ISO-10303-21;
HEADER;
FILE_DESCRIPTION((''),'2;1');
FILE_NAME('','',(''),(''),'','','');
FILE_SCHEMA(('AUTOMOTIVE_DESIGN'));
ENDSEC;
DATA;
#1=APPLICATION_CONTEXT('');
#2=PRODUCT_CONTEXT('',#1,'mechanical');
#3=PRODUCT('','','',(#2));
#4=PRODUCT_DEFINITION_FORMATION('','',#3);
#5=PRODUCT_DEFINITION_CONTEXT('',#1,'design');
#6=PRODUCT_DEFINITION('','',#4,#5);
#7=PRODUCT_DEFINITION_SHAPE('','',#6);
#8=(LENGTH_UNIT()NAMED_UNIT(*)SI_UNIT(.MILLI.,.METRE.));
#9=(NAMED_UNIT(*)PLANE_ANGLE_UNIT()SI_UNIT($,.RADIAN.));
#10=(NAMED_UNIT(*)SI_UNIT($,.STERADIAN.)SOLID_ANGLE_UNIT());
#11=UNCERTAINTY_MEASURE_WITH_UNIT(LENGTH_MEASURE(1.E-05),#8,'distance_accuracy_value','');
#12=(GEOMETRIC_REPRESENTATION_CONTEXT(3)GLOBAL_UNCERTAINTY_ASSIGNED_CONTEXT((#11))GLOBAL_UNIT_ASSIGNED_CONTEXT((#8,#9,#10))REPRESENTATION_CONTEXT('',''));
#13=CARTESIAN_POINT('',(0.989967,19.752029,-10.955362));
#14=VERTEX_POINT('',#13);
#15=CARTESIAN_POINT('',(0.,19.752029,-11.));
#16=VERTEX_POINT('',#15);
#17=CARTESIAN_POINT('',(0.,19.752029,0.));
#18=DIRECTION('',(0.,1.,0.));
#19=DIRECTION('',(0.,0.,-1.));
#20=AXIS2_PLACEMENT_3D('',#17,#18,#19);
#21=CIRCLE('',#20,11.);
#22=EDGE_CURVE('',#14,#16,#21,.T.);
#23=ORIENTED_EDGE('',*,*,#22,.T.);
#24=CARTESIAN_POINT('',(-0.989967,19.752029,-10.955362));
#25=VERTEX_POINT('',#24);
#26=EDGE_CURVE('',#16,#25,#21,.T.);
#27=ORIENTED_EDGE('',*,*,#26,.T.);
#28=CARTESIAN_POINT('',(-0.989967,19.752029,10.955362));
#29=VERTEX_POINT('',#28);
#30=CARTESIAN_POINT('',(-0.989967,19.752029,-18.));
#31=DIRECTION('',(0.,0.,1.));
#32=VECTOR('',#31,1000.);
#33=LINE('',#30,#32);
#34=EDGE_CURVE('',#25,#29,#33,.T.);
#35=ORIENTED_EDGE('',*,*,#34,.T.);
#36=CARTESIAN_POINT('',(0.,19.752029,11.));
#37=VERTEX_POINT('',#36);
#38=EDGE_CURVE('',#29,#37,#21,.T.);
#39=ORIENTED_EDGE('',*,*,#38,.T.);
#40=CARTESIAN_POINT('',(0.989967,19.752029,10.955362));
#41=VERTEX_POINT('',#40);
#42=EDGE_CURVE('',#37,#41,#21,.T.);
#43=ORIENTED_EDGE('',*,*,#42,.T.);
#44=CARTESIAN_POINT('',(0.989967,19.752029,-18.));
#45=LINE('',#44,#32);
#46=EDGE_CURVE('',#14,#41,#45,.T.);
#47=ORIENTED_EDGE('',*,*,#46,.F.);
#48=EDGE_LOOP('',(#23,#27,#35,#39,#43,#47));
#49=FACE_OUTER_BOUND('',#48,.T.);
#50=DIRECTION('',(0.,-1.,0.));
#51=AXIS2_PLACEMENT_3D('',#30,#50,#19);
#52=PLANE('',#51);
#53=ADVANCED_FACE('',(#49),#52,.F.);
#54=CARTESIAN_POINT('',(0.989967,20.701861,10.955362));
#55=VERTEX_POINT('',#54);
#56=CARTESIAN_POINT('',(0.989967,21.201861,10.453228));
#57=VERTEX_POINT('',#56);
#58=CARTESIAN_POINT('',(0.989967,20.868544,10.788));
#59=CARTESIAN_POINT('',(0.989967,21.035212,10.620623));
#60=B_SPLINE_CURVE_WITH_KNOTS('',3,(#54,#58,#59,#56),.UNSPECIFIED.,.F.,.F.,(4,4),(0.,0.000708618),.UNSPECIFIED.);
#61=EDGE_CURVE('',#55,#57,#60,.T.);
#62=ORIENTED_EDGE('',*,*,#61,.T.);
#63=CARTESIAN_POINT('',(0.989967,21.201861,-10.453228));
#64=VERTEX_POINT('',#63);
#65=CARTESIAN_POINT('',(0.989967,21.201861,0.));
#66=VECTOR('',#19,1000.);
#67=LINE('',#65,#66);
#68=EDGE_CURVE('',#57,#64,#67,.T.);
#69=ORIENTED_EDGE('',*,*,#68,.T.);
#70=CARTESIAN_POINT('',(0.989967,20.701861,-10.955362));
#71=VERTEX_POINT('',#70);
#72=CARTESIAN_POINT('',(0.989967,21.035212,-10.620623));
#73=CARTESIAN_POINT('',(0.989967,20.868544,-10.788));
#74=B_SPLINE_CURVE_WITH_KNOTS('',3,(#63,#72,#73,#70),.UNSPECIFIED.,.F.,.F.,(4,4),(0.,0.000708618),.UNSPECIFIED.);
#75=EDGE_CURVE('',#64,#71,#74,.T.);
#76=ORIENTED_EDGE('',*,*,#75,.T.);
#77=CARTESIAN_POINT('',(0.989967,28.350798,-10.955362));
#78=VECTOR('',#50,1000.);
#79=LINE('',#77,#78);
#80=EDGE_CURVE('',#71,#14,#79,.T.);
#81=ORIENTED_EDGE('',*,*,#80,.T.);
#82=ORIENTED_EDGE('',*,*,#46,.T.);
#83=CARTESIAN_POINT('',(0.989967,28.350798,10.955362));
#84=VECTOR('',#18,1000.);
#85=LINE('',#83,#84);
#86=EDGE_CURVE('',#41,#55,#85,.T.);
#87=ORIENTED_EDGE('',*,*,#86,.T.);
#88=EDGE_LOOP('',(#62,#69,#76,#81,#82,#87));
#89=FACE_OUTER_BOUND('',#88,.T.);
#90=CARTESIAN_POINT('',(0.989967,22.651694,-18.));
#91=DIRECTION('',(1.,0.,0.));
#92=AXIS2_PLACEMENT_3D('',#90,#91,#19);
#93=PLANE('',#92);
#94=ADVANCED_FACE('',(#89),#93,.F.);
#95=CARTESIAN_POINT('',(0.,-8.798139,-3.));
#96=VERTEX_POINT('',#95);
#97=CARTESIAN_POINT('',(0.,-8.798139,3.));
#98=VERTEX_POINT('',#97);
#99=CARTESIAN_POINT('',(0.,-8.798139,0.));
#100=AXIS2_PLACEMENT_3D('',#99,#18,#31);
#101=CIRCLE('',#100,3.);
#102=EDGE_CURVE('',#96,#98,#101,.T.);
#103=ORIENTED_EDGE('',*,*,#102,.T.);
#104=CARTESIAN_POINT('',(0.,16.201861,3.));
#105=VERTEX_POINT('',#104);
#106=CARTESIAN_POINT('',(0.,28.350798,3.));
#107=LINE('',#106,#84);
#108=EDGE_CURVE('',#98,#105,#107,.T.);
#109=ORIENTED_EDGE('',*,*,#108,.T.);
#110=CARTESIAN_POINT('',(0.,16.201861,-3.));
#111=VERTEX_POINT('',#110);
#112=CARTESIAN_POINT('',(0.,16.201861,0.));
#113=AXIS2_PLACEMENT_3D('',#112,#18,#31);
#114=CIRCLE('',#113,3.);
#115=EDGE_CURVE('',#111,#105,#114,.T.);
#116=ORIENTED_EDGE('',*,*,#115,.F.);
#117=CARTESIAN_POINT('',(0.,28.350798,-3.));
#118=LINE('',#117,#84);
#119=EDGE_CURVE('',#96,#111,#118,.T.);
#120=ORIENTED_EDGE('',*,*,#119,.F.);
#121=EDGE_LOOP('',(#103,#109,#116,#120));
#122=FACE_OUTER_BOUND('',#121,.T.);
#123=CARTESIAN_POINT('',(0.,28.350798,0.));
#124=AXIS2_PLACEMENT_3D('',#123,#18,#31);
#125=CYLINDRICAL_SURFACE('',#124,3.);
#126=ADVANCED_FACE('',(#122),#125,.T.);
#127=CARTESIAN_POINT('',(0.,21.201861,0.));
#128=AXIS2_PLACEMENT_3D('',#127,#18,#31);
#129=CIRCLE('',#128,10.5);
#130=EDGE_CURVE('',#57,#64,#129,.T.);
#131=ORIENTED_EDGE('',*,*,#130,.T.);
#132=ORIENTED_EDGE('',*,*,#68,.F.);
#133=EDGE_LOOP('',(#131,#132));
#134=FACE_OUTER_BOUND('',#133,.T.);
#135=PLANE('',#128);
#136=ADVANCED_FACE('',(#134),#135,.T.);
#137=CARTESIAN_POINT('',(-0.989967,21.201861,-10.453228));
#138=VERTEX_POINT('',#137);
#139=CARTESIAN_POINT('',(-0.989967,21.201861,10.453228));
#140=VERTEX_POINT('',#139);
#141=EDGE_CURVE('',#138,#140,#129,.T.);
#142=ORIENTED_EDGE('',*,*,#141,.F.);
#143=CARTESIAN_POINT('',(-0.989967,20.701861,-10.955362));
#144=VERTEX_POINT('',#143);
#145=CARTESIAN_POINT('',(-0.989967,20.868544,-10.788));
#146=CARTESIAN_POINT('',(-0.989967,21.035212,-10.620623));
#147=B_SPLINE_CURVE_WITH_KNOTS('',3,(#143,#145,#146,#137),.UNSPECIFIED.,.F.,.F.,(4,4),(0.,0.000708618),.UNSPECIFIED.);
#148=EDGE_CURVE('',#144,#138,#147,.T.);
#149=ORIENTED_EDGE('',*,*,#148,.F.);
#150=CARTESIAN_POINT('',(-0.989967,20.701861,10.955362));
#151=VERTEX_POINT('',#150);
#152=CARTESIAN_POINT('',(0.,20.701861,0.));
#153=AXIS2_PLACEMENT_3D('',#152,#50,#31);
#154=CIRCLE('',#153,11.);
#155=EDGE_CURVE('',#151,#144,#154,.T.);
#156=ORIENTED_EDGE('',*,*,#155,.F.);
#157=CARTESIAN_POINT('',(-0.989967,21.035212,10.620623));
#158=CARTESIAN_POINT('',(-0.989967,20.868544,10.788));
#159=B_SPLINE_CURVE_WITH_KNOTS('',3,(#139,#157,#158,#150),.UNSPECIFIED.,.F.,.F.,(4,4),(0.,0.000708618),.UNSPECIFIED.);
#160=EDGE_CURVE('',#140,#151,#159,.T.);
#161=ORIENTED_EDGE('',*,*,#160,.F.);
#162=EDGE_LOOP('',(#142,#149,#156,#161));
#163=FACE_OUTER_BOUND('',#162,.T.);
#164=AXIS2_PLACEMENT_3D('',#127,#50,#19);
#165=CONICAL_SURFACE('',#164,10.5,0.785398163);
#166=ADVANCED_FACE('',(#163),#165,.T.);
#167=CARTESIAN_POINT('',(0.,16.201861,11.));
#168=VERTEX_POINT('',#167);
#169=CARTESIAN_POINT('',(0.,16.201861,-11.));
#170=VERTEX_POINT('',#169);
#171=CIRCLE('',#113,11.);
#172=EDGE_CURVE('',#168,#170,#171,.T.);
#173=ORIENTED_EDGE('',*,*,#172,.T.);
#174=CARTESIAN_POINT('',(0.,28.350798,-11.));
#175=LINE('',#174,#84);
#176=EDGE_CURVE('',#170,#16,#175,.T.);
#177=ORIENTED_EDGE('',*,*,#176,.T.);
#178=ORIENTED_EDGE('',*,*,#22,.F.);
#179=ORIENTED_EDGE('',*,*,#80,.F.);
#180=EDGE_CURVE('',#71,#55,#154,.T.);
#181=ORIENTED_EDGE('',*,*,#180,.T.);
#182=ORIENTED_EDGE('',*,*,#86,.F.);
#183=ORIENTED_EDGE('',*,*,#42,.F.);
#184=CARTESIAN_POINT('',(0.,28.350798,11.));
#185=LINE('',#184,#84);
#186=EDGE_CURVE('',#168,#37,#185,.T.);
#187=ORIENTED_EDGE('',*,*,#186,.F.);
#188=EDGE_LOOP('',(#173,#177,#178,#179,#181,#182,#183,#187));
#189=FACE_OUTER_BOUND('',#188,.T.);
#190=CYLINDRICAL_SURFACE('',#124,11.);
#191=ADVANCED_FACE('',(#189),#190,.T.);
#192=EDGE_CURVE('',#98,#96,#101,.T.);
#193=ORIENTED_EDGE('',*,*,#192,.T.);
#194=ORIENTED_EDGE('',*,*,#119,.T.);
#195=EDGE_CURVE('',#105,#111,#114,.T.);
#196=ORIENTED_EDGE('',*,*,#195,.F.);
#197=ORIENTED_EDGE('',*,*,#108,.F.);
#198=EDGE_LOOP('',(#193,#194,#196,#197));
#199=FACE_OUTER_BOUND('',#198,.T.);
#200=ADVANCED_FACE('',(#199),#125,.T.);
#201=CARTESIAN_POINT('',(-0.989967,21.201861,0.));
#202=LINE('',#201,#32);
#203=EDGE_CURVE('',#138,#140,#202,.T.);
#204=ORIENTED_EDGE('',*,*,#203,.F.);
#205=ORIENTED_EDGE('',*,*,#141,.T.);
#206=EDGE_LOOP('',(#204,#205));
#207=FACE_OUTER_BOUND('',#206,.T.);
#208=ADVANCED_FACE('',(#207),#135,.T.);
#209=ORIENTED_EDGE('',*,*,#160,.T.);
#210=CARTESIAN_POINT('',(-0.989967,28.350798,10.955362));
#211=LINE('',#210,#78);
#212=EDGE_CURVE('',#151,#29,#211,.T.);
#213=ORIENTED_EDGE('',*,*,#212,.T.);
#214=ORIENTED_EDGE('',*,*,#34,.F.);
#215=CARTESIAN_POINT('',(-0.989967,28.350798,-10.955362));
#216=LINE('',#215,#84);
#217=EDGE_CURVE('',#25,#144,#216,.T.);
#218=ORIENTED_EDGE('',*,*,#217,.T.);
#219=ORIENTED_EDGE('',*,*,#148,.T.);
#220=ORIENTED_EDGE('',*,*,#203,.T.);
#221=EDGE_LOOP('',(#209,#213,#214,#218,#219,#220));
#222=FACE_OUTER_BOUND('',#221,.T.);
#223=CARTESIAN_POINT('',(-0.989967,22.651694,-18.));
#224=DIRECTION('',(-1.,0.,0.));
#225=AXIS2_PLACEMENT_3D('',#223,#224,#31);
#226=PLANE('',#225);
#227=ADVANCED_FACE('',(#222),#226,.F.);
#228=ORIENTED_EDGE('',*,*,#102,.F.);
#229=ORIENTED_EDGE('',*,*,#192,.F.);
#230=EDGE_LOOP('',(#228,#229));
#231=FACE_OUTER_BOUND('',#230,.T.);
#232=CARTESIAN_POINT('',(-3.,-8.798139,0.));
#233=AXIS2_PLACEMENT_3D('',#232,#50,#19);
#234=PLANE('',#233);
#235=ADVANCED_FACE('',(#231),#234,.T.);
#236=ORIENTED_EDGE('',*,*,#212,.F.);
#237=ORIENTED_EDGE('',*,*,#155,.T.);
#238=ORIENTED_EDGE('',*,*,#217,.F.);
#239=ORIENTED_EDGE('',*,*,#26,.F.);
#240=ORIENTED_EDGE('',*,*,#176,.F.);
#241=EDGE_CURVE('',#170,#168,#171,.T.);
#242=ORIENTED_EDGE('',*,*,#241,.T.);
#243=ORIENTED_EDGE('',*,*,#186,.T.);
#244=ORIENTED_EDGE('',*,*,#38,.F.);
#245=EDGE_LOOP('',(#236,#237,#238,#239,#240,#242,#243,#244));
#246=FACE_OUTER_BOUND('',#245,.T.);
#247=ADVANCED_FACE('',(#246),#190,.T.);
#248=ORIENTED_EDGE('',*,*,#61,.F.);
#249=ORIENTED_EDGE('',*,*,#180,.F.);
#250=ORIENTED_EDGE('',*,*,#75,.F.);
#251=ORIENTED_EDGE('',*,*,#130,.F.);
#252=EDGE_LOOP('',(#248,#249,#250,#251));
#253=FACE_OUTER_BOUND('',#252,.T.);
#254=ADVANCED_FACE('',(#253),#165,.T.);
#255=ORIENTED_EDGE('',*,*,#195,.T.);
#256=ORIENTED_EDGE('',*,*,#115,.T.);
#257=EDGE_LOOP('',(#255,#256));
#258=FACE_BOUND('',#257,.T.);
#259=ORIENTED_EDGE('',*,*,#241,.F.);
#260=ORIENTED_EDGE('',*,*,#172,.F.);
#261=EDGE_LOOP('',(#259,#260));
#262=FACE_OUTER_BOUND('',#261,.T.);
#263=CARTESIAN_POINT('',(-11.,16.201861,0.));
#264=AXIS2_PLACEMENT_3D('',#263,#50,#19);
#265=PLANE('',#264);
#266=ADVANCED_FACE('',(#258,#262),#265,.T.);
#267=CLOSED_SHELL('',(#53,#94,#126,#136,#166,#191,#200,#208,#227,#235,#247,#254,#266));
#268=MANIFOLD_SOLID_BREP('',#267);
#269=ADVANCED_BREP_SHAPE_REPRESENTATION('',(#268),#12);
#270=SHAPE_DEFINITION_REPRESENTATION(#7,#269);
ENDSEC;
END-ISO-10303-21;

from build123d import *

# Parameters (mm, degrees)
SKETCH2_W          = 1.97993319
SKETCH2_H          = 2.899664475
CUT_EXTRUDE1_DEPTH = 18
CHAMFER1_SIZE      = 0.5


with BuildPart() as part:
    # Sketch1 → Revolve1 (revolve)
    with BuildSketch(Plane.XY, mode=Mode.PRIVATE) as revolve1_sk:
        Polygon((0, 21.201861416), (-11, 21.201861416), (-11, 16.201861416), (-3, 16.201861416), (-3, -8.798138584), (0, -8.798138584), align=None)
    revolve(revolve1_sk.sketch.rotate(Axis((0, 28.350797586, 0), (0, -1, 0)), 270), axis=Axis((0, 28.350797586, 0), (0, -1, 0)))

    # Sketch2 → Cut-Extrude1 (cut, symmetric)
    with BuildSketch(Plane.XY):
        with Locations((0, 21.201861416)):
            Rectangle(SKETCH2_W, SKETCH2_H)
    extrude(amount=CUT_EXTRUDE1_DEPTH, both=True, mode=Mode.SUBTRACT)

    # Chamfer1
    chamfer1_edges = [part.edges().sort_by_distance(p)[0] for p in [
        (-11, 21.201861416, 0),
        (11, 21.201861416, 0),
    ]]
    chamfer(chamfer1_edges, length=CHAMFER1_SIZE)


solid = part.part
